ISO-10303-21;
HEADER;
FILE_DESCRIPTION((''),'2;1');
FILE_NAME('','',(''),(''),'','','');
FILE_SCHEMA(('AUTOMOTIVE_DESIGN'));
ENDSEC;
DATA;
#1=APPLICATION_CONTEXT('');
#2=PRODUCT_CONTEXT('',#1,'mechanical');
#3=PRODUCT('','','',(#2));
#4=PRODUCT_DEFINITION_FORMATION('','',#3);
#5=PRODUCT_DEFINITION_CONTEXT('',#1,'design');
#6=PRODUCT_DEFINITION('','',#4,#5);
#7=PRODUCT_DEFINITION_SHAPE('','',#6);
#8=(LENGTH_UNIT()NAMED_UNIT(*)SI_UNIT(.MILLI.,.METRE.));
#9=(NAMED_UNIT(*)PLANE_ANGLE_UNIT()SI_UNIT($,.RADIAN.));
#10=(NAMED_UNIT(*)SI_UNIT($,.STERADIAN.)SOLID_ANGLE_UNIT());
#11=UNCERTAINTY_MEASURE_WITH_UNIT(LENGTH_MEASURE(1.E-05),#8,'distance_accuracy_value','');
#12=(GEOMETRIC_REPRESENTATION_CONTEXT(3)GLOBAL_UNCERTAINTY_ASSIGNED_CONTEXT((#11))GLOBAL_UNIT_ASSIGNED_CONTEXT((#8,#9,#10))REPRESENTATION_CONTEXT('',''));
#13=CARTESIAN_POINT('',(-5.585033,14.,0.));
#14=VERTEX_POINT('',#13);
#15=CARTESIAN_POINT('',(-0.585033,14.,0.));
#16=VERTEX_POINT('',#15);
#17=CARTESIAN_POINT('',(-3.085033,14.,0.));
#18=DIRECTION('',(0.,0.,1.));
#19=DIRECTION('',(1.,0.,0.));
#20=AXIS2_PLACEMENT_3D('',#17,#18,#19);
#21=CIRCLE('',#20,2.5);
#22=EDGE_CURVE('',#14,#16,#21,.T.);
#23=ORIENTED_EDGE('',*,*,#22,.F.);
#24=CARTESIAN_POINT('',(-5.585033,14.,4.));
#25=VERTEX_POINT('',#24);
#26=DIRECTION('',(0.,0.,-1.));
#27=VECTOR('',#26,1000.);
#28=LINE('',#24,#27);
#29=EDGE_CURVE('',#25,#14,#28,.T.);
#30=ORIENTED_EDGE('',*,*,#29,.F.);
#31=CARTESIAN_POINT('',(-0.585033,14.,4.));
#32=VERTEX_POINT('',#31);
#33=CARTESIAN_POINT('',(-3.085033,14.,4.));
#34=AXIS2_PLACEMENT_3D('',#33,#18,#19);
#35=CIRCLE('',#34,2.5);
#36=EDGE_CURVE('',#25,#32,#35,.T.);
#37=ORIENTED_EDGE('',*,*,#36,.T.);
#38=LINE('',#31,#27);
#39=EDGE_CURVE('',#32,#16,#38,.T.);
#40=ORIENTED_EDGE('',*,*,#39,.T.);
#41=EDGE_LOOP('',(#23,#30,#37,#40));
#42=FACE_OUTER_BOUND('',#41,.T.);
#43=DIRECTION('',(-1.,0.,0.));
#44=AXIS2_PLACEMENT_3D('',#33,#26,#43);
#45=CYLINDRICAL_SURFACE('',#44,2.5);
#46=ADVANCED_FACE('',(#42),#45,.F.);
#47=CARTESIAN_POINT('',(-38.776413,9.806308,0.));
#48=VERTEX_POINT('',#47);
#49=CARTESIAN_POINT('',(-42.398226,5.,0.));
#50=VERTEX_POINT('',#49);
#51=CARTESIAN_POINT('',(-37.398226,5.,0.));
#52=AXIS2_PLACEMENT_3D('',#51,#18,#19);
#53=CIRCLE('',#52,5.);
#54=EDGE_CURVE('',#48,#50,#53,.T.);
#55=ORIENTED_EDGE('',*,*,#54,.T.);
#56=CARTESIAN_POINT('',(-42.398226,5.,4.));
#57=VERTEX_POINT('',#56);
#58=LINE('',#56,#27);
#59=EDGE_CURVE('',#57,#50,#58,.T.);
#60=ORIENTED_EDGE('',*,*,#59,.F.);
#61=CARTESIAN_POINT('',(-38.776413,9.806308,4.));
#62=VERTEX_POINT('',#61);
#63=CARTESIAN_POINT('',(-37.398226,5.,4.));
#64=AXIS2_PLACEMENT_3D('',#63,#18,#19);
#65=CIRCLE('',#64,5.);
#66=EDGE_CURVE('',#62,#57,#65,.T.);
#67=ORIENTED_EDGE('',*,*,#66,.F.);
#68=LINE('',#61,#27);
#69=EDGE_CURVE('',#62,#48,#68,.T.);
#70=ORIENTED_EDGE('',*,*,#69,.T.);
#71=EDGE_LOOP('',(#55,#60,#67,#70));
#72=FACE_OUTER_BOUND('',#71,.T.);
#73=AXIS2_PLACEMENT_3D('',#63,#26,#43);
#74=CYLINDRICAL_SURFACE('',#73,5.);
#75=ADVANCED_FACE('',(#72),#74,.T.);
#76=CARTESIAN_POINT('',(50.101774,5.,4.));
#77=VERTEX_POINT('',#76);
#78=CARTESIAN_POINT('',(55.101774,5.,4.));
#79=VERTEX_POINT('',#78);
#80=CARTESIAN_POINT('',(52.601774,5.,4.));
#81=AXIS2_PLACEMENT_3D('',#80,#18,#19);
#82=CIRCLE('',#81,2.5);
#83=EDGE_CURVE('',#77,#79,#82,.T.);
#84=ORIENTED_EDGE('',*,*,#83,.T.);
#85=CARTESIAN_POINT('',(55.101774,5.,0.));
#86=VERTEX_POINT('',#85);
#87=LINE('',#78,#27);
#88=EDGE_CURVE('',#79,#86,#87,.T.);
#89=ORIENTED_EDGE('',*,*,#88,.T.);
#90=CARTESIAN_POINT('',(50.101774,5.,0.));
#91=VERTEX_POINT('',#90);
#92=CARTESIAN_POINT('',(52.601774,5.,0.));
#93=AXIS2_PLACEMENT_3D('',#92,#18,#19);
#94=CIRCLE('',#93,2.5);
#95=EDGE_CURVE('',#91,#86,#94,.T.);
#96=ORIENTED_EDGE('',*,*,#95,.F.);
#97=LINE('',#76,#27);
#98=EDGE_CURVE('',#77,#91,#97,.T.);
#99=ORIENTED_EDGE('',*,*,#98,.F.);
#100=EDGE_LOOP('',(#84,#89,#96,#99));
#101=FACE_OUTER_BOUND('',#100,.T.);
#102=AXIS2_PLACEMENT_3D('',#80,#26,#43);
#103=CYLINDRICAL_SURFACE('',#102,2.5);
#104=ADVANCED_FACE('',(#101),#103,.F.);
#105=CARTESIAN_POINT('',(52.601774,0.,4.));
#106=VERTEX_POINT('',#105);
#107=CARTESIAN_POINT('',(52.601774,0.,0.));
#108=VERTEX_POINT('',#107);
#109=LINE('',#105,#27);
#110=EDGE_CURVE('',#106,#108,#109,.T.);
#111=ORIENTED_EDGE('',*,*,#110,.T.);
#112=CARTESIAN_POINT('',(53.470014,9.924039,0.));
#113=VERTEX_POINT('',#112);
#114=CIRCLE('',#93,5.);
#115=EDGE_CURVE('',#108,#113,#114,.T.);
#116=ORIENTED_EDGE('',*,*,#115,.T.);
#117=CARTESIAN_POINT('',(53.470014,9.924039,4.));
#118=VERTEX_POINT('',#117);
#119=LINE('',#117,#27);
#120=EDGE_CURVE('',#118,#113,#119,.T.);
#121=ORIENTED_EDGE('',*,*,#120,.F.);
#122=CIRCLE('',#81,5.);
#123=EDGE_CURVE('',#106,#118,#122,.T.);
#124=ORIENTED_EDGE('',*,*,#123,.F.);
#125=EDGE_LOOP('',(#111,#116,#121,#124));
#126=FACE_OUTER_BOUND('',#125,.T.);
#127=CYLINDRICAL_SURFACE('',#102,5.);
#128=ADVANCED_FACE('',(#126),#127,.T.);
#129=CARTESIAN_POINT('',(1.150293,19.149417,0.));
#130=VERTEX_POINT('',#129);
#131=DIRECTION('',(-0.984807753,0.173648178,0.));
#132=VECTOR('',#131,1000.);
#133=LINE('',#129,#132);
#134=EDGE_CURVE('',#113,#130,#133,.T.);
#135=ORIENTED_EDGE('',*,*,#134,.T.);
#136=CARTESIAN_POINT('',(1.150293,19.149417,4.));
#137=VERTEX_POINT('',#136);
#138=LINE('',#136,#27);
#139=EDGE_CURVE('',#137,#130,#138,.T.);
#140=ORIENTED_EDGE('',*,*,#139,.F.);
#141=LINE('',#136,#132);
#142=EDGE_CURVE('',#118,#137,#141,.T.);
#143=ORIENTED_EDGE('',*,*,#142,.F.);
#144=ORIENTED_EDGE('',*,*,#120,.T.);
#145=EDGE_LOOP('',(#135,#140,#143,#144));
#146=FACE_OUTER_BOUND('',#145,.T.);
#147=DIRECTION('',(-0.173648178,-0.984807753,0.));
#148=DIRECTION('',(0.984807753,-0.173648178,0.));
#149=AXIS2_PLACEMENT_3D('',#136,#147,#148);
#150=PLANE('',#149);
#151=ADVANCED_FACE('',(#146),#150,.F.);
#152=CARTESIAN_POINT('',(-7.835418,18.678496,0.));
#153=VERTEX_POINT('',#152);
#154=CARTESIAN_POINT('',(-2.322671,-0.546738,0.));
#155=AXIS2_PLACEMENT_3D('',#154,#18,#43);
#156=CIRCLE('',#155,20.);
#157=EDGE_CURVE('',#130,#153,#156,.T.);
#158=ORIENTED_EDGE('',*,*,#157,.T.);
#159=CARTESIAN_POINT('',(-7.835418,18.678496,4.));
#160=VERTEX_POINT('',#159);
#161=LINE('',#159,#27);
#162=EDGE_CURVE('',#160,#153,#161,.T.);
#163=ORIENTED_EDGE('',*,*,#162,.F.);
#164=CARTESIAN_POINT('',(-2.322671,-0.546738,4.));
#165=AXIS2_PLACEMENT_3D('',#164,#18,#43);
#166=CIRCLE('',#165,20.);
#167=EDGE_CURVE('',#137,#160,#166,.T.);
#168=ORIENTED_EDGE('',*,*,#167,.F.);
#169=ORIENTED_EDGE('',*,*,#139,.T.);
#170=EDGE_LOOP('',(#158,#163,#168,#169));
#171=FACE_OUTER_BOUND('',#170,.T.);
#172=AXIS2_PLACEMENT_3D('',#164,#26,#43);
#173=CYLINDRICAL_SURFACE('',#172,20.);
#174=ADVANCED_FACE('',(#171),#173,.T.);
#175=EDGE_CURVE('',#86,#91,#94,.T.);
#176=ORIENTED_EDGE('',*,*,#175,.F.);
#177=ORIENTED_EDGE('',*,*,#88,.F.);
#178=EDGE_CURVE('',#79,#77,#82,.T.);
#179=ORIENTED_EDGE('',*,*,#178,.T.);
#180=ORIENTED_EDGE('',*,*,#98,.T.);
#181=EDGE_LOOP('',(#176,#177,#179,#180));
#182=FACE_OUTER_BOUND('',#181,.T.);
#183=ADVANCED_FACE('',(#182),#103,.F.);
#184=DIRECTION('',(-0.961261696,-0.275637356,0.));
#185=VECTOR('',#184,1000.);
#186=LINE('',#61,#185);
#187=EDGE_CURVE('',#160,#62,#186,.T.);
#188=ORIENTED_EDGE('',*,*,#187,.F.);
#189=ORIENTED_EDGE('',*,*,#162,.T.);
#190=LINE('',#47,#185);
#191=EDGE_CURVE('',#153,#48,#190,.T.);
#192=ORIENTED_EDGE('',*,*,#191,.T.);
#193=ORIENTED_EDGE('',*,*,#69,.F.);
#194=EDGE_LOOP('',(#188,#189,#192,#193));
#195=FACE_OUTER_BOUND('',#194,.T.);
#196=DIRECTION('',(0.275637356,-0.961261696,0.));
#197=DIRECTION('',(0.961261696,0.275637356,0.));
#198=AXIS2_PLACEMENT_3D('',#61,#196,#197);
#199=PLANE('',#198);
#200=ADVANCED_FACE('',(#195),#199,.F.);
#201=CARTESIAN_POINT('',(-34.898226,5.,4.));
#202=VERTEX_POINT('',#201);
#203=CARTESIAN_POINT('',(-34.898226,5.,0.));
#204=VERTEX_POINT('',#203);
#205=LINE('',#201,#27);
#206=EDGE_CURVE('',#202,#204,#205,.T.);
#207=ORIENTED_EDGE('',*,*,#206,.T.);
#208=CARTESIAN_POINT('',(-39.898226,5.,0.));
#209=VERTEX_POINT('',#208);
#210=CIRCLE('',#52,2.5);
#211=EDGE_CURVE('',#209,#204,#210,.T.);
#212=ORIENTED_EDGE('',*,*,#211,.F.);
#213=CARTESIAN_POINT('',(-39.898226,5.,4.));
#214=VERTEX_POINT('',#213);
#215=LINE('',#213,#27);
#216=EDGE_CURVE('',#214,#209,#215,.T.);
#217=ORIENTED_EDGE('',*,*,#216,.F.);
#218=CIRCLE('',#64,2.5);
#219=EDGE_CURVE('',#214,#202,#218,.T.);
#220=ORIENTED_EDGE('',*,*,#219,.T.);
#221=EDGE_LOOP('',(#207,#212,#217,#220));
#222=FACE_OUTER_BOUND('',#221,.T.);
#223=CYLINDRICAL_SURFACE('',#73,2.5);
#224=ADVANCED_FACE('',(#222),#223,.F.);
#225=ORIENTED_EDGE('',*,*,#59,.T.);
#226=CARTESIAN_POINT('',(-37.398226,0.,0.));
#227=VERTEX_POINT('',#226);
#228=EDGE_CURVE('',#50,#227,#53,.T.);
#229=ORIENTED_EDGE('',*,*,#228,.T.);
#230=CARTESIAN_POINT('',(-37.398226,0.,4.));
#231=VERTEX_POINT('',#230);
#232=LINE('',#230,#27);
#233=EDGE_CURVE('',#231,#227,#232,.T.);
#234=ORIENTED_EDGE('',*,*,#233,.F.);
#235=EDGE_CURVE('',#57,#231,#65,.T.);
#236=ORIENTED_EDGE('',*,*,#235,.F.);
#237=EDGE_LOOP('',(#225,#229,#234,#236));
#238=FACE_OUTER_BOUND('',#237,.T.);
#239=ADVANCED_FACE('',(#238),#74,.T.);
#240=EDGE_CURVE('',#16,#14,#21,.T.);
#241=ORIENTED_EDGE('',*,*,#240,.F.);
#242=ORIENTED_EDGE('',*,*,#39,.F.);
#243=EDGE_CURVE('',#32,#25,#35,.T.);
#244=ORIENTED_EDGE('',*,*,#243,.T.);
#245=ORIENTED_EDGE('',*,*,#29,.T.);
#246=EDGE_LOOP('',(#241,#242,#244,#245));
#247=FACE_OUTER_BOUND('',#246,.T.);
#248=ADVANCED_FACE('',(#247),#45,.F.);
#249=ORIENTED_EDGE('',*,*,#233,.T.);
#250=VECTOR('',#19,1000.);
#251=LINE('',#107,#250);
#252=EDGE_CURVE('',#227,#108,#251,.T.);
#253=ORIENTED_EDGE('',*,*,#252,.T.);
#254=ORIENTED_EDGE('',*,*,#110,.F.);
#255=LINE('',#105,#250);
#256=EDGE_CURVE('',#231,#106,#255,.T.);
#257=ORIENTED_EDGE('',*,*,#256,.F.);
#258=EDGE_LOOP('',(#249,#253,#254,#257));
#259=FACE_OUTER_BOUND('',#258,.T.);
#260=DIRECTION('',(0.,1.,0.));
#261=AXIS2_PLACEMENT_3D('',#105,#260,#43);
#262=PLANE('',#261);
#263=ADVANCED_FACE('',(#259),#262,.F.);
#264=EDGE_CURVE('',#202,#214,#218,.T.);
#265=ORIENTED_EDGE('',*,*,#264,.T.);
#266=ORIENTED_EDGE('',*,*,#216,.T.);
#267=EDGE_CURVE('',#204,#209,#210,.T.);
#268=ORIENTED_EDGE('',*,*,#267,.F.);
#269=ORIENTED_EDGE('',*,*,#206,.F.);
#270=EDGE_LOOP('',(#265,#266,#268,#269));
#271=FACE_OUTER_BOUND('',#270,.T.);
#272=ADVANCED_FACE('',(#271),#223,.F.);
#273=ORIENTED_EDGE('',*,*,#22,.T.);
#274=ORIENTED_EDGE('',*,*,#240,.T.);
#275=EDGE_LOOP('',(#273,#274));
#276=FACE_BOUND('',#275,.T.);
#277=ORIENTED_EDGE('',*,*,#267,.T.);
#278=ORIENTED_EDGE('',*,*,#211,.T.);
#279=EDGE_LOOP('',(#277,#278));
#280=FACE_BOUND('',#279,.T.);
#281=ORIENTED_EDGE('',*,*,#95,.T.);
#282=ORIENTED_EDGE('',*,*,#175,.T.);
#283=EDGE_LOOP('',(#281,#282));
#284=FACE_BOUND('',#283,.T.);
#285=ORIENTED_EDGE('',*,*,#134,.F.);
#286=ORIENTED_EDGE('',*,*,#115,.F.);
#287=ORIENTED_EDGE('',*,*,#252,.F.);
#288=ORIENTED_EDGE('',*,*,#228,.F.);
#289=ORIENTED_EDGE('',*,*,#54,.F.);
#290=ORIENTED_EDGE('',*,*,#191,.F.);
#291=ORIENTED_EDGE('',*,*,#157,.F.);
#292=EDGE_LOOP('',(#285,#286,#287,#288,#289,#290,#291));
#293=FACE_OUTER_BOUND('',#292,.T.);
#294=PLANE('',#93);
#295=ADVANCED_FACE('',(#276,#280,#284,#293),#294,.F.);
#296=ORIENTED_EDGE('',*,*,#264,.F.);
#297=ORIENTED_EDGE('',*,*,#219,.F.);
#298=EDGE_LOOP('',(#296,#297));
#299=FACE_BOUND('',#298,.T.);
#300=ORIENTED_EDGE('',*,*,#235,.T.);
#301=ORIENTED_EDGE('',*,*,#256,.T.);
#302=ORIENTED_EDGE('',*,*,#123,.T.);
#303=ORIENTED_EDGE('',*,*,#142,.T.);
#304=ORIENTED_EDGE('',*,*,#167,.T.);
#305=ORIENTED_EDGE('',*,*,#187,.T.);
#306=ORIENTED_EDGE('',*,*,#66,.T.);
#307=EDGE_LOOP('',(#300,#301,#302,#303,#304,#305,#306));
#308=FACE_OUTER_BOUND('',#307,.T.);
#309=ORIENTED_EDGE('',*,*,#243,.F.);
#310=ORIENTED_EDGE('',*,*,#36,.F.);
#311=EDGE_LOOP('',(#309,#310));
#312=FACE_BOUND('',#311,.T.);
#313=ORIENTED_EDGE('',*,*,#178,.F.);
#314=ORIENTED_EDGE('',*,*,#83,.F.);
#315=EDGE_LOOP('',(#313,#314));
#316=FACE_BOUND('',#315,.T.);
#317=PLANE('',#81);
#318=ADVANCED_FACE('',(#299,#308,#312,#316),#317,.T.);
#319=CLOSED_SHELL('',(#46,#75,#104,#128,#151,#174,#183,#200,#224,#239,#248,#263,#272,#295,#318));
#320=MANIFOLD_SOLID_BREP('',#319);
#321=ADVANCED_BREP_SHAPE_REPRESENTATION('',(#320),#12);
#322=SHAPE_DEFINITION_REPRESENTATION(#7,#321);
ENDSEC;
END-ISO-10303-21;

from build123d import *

# Parameters (mm, degrees)
LINK_PROFILE_SKETCH_R = 2.5
LINK_PLATE_4MM_DEPTH  = 4


with BuildPart() as part:
    # Link Profile Sketch → Link Plate 4mm (new body)
    with BuildSketch(Plane.XY):
        with BuildLine():
            Line((52.601773573, 0), (-37.398226427, 0))
            ThreePointArc((-37.398226427, 0), (-42.349566771, 4.304134495), (-38.776413207, 9.80630848))
            Line((-38.776413207, 9.80630848), (-7.835417757, 18.678496156))
            ThreePointArc((-7.835417757, 18.678496156), (-3.369389765, 19.425852932), (1.150292913, 19.149417297))
            Line((1.150292913, 19.149417297), (53.470014461, 9.924038765))
            ThreePointArc((53.470014461, 9.924038765), (57.582747063, 4.564221286), (52.601773573, 0))
        make_face()
        with Locations((-3.085032863, 14)):
            Circle(LINK_PROFILE_SKETCH_R, mode=Mode.SUBTRACT)
        with Locations((-37.398226427, 5)):
            Circle(LINK_PROFILE_SKETCH_R, mode=Mode.SUBTRACT)
        with Locations((52.601773573, 5)):
            Circle(LINK_PROFILE_SKETCH_R, mode=Mode.SUBTRACT)
    extrude(amount=LINK_PLATE_4MM_DEPTH)


solid = part.part
